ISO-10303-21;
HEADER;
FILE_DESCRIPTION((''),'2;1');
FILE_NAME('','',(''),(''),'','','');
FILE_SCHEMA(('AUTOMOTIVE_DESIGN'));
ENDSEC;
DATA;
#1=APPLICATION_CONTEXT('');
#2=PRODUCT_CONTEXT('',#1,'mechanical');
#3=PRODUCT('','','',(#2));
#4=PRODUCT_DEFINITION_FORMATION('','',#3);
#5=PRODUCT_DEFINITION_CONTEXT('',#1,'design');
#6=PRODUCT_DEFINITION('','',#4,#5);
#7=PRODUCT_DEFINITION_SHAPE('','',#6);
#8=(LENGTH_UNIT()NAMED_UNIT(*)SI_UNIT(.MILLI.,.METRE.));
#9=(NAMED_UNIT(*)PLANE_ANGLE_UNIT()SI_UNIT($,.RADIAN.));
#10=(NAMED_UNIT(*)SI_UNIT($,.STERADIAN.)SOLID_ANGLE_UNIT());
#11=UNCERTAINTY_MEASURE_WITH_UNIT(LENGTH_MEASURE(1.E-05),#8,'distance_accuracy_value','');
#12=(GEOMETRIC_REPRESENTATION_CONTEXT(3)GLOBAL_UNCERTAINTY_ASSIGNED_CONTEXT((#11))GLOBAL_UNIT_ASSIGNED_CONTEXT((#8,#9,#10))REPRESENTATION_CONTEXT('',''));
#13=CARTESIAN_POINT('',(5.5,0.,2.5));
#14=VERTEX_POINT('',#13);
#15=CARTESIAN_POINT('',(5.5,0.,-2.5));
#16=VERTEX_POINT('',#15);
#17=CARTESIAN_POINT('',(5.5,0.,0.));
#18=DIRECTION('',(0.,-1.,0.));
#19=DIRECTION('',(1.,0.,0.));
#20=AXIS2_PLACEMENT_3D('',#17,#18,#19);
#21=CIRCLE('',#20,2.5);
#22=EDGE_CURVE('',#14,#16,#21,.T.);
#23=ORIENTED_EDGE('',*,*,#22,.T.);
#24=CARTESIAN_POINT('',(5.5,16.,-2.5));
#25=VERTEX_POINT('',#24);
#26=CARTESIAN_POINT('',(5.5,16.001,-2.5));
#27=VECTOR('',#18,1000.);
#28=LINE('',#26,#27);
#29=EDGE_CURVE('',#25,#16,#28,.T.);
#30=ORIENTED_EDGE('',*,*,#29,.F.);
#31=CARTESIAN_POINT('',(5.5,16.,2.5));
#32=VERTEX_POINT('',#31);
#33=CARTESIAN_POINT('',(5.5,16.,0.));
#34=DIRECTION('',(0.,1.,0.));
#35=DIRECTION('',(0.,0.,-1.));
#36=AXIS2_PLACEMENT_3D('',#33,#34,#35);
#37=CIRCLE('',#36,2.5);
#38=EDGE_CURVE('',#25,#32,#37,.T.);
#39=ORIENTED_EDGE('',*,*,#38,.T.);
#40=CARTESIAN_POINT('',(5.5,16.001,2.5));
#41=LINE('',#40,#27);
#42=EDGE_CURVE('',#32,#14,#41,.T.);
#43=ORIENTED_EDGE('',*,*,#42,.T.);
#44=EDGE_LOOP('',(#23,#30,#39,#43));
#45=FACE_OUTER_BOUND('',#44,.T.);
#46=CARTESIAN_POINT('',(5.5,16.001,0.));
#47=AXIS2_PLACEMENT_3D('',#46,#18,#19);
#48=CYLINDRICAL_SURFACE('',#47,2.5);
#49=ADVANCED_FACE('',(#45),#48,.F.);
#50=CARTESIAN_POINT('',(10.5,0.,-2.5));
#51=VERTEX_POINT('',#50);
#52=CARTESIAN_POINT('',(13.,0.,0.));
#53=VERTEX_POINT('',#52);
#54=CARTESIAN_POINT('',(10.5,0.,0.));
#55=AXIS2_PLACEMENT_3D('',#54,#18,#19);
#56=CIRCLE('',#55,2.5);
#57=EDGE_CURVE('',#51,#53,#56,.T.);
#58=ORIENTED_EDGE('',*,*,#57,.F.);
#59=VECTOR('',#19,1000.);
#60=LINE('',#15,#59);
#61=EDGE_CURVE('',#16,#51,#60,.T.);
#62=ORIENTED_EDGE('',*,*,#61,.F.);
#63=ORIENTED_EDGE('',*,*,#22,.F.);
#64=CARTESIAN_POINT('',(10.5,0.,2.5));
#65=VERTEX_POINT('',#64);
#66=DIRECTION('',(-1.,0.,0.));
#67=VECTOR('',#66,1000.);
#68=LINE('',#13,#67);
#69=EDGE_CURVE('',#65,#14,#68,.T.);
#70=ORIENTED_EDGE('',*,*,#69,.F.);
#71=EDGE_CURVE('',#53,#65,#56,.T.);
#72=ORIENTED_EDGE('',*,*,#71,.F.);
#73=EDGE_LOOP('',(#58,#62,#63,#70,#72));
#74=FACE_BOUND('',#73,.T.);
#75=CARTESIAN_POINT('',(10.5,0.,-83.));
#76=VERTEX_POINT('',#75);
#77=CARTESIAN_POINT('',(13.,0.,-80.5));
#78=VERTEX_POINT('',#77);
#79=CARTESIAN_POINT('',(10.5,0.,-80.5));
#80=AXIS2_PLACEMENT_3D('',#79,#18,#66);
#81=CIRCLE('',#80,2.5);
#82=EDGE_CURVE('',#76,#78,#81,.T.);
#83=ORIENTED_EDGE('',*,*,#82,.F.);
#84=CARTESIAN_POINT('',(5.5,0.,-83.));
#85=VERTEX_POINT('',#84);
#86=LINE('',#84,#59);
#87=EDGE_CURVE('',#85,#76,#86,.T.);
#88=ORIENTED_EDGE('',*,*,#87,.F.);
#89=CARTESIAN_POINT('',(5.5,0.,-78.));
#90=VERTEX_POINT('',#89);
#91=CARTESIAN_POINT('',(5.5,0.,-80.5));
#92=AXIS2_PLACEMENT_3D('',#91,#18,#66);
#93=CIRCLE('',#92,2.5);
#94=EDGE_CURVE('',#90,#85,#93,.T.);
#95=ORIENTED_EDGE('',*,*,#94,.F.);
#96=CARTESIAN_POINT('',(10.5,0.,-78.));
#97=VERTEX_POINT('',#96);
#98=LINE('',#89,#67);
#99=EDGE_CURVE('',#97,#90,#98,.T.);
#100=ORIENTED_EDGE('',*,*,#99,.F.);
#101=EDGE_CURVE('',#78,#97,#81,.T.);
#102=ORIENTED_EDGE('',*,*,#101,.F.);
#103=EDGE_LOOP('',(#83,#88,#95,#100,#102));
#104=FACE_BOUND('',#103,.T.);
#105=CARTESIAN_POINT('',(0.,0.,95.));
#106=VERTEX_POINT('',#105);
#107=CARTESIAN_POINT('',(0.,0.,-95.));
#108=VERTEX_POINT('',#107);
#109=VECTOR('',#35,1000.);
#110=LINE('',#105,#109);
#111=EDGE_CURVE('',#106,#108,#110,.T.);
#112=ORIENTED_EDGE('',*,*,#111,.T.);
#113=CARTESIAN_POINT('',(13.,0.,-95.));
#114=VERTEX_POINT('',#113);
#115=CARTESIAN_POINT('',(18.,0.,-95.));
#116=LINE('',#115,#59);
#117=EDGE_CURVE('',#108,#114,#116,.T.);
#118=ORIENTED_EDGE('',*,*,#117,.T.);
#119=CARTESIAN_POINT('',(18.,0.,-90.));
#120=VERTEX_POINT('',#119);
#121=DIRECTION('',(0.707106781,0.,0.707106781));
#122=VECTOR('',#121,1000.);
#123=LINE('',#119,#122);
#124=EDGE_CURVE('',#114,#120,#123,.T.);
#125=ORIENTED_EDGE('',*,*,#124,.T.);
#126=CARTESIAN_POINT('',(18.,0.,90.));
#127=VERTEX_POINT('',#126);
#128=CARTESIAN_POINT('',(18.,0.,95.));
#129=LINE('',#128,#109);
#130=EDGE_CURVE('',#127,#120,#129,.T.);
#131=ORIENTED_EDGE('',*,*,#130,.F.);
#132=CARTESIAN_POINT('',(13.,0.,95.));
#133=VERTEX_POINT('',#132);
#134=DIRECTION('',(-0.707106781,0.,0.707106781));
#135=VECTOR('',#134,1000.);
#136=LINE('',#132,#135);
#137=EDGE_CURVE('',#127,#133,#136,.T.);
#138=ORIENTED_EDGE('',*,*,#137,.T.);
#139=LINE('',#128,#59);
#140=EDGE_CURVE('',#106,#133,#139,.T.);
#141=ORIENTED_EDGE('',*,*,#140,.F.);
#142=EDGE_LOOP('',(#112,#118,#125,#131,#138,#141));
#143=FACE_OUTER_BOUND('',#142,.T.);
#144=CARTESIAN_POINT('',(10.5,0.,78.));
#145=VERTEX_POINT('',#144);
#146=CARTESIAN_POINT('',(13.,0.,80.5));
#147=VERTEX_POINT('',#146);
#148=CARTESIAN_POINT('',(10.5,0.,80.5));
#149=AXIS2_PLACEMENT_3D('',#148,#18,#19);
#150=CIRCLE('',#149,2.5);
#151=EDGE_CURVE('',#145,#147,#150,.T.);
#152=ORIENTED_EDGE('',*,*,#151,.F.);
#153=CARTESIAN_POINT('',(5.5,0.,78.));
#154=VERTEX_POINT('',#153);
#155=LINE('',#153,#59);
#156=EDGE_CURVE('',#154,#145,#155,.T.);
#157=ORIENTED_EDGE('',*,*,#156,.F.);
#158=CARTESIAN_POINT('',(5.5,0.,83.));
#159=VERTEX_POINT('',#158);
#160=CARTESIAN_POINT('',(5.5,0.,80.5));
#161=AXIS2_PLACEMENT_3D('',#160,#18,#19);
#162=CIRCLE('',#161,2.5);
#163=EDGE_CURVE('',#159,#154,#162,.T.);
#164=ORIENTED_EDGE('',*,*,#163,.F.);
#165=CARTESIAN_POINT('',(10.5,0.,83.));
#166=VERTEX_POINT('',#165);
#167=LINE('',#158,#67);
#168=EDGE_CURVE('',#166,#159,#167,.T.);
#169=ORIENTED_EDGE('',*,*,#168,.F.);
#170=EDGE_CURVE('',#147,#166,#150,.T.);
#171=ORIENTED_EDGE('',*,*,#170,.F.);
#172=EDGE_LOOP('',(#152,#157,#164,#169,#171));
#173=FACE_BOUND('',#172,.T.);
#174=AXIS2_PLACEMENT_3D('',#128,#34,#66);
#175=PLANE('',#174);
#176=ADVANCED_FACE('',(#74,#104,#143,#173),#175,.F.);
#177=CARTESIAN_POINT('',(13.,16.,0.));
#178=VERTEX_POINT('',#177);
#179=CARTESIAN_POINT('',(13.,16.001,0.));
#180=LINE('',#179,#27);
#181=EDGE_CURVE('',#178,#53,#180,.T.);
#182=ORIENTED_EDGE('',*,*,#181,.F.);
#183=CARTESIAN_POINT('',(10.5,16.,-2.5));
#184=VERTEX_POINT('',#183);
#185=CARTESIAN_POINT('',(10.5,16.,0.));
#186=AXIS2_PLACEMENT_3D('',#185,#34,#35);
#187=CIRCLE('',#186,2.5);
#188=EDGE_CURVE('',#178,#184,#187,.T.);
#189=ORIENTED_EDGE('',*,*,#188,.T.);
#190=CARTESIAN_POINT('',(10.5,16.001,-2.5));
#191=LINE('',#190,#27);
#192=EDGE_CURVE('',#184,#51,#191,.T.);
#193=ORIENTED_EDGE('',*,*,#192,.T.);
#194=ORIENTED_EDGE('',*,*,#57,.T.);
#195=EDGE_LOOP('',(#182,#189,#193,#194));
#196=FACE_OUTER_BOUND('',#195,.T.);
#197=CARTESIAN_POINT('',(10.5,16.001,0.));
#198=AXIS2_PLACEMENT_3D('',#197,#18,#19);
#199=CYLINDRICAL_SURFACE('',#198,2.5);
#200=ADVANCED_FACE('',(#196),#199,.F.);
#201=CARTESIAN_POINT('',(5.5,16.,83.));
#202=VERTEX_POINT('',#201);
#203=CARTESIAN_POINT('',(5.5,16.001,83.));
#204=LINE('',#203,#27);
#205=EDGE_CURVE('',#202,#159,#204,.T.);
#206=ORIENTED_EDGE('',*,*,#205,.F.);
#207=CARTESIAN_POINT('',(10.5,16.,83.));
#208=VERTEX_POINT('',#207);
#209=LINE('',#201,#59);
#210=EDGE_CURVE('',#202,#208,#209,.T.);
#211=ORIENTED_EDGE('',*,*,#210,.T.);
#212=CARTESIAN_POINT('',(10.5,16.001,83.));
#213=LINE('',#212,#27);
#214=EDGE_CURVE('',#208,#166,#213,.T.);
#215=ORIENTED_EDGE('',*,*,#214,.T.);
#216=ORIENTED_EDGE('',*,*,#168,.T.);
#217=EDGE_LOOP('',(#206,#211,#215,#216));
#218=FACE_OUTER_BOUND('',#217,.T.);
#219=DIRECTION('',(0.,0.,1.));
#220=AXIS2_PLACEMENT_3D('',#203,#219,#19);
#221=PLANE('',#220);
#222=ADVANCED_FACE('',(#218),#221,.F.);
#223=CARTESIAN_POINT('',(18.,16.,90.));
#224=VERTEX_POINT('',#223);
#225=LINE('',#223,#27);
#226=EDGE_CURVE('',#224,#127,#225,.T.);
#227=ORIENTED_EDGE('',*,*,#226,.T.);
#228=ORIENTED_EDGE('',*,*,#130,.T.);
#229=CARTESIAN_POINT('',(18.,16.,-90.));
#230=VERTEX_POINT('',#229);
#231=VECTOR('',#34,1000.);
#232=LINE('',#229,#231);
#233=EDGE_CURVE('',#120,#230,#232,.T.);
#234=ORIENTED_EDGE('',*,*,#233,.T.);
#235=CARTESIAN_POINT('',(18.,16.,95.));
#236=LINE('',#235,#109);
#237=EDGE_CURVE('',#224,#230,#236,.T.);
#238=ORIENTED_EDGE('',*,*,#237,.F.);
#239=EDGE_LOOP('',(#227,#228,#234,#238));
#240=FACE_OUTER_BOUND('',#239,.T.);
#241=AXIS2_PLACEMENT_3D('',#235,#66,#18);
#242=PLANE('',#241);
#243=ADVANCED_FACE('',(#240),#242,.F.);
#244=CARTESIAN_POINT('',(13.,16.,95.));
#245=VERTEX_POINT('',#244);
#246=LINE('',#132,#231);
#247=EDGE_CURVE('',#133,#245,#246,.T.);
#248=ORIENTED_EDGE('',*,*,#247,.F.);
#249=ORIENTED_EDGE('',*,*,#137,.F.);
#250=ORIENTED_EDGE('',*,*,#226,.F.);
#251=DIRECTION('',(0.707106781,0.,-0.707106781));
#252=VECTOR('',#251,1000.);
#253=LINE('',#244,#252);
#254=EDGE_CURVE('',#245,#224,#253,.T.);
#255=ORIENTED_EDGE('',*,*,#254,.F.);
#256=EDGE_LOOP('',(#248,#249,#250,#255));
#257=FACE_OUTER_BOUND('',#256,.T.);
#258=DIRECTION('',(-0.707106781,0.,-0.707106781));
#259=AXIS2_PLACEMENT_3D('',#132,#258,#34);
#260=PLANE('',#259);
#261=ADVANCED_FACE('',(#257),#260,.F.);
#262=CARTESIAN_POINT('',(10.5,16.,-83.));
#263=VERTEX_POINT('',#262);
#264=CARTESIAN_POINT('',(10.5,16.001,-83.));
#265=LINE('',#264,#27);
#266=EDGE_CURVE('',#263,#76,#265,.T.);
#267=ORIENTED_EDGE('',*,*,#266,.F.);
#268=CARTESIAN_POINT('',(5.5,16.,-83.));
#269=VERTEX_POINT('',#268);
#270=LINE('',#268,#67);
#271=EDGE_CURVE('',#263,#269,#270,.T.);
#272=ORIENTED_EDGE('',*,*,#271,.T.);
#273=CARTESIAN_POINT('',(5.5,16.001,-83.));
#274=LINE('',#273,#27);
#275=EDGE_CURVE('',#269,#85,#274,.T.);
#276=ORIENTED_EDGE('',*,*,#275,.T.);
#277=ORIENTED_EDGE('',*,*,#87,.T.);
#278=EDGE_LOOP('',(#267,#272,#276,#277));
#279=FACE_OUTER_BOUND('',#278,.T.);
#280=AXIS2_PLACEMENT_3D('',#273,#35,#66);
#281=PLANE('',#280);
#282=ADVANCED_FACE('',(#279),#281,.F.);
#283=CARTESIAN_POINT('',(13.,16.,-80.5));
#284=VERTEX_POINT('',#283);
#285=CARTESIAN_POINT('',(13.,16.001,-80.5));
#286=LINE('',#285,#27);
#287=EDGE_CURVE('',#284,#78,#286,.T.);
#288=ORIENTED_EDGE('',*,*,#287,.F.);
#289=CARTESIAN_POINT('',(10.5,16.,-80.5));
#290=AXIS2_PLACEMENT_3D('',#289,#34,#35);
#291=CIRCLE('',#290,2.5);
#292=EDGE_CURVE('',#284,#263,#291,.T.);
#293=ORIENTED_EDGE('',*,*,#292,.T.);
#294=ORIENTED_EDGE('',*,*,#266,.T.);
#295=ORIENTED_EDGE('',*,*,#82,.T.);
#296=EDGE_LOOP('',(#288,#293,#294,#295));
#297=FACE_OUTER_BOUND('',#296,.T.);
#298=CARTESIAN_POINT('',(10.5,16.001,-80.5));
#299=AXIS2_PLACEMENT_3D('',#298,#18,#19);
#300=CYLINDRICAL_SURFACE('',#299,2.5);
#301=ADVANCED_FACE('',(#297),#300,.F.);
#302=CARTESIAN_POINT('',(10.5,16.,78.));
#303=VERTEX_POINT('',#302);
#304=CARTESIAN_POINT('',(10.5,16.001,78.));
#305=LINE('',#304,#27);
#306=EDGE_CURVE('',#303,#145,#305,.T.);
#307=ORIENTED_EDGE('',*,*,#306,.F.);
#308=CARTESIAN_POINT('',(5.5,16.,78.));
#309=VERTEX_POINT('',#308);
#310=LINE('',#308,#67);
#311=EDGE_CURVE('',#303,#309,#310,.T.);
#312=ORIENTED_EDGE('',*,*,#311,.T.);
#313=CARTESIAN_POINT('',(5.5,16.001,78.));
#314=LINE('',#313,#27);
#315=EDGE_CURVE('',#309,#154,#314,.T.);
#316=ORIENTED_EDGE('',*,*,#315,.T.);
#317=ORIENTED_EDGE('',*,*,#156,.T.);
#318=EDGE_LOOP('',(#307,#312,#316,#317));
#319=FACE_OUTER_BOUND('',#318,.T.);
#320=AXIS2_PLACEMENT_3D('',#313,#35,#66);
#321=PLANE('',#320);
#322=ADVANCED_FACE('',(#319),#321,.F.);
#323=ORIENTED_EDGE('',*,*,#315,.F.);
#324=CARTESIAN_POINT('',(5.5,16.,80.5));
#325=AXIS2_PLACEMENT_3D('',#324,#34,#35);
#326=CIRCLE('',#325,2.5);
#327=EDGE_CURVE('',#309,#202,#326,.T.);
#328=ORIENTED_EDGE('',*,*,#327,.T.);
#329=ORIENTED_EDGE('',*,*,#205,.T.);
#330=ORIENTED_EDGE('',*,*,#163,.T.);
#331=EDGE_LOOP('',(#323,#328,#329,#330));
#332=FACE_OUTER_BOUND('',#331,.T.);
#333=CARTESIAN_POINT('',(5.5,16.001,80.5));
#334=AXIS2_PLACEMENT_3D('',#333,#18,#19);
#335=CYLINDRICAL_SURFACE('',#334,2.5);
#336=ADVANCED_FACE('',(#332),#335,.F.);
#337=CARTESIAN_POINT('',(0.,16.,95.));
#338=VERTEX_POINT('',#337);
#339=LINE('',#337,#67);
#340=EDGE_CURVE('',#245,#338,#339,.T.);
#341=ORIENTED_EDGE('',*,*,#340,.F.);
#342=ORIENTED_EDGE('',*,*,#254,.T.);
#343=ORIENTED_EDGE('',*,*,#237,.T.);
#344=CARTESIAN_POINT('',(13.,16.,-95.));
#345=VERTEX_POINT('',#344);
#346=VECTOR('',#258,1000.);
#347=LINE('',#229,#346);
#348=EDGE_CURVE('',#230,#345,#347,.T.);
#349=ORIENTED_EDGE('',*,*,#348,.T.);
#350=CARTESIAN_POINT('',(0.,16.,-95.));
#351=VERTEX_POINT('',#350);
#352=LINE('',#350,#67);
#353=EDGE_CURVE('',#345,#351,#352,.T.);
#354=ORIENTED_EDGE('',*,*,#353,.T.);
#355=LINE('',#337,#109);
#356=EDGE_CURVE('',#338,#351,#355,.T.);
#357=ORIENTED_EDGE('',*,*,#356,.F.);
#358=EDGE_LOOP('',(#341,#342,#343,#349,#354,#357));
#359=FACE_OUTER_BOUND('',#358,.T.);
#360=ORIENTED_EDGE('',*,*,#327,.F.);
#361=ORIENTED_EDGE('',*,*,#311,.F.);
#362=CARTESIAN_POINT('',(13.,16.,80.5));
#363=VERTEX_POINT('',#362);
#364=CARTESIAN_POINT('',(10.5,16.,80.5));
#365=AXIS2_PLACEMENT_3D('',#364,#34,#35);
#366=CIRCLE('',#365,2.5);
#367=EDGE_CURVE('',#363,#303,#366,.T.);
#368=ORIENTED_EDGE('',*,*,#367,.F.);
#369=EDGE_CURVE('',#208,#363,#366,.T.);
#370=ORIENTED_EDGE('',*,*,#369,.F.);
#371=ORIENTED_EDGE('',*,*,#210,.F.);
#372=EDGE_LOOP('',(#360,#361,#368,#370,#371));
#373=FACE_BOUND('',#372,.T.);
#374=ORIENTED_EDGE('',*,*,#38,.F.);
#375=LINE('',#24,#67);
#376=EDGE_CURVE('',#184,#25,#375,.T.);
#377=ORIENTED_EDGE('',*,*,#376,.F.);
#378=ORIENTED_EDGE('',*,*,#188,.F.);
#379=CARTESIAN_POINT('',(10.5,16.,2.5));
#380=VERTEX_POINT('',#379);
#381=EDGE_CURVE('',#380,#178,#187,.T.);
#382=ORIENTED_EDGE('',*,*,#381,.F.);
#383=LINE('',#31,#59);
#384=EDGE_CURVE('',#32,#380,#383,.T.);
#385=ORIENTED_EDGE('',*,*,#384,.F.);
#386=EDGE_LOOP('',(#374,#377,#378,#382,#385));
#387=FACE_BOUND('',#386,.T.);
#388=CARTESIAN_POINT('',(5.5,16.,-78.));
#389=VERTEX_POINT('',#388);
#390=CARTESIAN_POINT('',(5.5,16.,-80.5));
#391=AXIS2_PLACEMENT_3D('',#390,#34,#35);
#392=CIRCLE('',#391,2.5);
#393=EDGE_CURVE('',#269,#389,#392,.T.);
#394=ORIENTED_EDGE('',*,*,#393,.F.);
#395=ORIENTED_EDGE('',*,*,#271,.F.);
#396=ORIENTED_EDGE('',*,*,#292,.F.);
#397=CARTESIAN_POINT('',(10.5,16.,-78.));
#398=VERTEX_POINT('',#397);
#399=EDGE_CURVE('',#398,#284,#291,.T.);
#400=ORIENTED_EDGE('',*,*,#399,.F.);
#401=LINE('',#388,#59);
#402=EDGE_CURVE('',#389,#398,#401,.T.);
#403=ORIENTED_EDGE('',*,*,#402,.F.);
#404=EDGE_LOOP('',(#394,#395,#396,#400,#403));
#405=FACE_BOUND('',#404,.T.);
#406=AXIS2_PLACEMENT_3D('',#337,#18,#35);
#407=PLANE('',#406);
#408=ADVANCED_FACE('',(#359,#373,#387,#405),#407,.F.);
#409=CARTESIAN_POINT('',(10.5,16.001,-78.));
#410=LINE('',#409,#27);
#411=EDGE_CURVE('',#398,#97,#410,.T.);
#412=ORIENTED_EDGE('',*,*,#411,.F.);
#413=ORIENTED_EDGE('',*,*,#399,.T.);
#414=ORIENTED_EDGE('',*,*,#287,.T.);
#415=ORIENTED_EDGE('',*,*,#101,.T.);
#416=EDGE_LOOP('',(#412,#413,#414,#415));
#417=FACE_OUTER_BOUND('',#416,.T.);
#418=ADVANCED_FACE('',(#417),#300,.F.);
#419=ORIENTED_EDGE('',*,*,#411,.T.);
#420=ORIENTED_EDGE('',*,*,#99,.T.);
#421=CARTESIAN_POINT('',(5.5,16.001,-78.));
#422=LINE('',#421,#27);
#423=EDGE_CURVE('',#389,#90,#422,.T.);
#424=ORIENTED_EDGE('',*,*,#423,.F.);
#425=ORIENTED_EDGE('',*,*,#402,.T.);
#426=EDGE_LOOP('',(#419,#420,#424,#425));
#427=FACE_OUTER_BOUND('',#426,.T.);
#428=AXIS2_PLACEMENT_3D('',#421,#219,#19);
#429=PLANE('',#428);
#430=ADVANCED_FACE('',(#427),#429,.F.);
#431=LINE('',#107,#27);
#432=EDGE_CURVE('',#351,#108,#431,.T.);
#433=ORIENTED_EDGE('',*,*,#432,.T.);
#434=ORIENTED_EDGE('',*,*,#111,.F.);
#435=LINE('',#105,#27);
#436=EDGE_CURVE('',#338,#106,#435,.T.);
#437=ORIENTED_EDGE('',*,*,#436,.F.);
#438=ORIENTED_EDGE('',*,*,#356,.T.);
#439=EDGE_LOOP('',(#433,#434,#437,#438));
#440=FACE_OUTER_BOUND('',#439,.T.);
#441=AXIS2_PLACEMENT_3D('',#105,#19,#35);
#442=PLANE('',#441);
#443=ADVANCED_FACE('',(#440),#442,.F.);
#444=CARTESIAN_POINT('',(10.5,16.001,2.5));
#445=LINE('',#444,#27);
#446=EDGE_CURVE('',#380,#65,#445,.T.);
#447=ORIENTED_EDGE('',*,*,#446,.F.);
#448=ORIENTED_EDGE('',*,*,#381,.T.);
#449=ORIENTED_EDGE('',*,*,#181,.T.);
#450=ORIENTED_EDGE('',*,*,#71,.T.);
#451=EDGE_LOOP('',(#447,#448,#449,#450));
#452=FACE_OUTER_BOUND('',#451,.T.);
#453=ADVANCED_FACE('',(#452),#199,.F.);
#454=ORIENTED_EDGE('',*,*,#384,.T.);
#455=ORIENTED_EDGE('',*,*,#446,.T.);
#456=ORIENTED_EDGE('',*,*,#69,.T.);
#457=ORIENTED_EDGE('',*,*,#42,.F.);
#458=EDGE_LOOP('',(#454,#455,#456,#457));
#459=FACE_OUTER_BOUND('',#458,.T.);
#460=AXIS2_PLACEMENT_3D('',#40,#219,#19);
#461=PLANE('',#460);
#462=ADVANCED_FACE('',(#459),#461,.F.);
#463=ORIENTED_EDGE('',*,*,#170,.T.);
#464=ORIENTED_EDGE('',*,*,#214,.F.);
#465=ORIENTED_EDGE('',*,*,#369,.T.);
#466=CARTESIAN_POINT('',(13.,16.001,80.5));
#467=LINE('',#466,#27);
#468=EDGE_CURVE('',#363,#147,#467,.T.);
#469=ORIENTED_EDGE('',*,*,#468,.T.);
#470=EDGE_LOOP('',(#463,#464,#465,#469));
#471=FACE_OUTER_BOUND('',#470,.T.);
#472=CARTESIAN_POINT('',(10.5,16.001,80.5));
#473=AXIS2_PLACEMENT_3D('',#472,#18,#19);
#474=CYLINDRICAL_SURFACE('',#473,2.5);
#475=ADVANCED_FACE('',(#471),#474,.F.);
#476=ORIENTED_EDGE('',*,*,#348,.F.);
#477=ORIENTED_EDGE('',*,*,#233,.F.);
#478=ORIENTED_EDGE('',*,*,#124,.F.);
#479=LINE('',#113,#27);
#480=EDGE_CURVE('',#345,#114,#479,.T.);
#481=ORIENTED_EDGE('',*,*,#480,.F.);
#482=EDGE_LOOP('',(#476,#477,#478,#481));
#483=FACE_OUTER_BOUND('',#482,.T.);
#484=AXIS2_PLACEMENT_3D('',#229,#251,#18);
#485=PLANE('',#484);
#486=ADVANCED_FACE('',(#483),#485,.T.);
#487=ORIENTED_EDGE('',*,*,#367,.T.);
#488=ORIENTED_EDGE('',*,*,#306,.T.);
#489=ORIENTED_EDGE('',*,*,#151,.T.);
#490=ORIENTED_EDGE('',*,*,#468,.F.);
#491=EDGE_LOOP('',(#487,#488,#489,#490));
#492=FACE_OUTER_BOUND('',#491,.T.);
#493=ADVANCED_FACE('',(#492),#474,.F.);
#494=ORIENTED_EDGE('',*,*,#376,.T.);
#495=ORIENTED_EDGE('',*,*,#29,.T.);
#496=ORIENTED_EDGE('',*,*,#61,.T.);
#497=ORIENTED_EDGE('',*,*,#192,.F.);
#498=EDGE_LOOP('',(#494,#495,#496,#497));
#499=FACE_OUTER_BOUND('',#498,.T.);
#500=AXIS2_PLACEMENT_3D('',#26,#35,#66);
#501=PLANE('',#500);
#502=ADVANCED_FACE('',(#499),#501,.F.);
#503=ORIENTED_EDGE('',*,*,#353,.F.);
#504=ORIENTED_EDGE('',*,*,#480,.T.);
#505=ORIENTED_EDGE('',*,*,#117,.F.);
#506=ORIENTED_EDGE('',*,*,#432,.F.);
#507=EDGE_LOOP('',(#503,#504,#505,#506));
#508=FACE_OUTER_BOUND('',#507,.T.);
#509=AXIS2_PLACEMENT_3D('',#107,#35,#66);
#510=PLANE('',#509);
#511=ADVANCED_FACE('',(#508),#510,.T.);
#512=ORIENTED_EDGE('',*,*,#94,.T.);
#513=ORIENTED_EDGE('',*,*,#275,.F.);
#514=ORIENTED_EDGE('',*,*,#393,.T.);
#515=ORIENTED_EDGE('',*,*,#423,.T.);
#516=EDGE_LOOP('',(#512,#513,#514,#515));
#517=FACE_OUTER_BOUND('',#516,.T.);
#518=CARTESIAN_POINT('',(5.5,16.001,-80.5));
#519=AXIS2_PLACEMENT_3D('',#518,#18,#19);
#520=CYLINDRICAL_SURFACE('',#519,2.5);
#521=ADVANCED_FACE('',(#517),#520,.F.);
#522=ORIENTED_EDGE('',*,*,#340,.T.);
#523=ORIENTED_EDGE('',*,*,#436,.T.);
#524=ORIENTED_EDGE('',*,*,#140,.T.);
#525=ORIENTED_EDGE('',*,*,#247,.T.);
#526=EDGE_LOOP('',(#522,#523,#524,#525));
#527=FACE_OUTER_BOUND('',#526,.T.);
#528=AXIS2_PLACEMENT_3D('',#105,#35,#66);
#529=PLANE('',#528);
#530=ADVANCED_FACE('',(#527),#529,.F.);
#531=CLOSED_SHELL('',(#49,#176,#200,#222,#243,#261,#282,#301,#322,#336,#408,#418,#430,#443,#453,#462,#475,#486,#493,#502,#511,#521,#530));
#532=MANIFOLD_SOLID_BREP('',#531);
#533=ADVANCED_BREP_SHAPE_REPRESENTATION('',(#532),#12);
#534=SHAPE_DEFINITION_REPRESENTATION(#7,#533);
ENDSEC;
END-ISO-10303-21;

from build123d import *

# Parameters (mm, degrees)
SKETCH_1_W          = 18
SKETCH_1_H          = 16
EXTRUDE_1_DEPTH     = 95
CHAMFER_1_SIZE      = 5
CUT_EXTRUDE_1_REACH = 100.005


with BuildPart() as part:
    # 草图1 → 凸台-拉伸1 (new, symmetric)
    with BuildSketch(Plane.XY):
        with Locations((9, 8)):
            Rectangle(SKETCH_1_W, SKETCH_1_H)
    extrude(amount=EXTRUDE_1_DEPTH, both=True)

    # 倒角1
    chamfer_1_edges = [part.edges().sort_by_distance(p)[0] for p in [
        (18, 8, -95),
        (18, 8, 95),
    ]]
    chamfer(chamfer_1_edges, length=CHAMFER_1_SIZE)

    # 草图2 → 切除-拉伸1 (cut, up to next)
    with BuildSketch(Plane.XZ, mode=Mode.PRIVATE) as cut_extrude_1_sk1:
        with BuildLine():
            Line((5.5, 83), (10.5, 83))
            ThreePointArc((10.5, 83), (13, 80.5), (10.5, 78))
            Line((10.5, 78), (5.5, 78))
            ThreePointArc((5.5, 78), (3, 80.5), (5.5, 83))
        make_face()
    cut_extrude_1_tool1 = extrude(cut_extrude_1_sk1.sketch, amount=-CUT_EXTRUDE_1_REACH, mode=Mode.PRIVATE) & part.part
    # 草图2 → 切除-拉伸1 (cut, up to next)
    with BuildSketch(Plane.XZ, mode=Mode.PRIVATE) as cut_extrude_1_sk2:
        with BuildLine():
            Line((5.5, 2.5), (10.5, 2.5))
            ThreePointArc((10.5, 2.5), (13, 0), (10.5, -2.5))
            Line((10.5, -2.5), (5.5, -2.5))
            ThreePointArc((5.5, -2.5), (3, 0), (5.5, 2.5))
        make_face()
    cut_extrude_1_tool2 = extrude(cut_extrude_1_sk2.sketch, amount=-CUT_EXTRUDE_1_REACH, mode=Mode.PRIVATE) & part.part
    # 草图2 → 切除-拉伸1 (cut, up to next)
    with BuildSketch(Plane.XZ, mode=Mode.PRIVATE) as cut_extrude_1_sk3:
        with BuildLine():
            Line((5.5, -83), (10.5, -83))
            ThreePointArc((10.5, -83), (13, -80.5), (10.5, -78))
            Line((10.5, -78), (5.5, -78))
            ThreePointArc((5.5, -78), (3, -80.5), (5.5, -83))
        make_face()
    cut_extrude_1_tool3 = extrude(cut_extrude_1_sk3.sketch, amount=-CUT_EXTRUDE_1_REACH, mode=Mode.PRIVATE) & part.part
    add(cut_extrude_1_tool1.solids().sort_by_distance((8, 0, 80.5))[0], mode=Mode.SUBTRACT)
    add(cut_extrude_1_tool2.solids().sort_by_distance((8, 0, 0))[0], mode=Mode.SUBTRACT)
    add(cut_extrude_1_tool3.solids().sort_by_distance((8, 0, -80.5))[0], mode=Mode.SUBTRACT)


solid = part.part
